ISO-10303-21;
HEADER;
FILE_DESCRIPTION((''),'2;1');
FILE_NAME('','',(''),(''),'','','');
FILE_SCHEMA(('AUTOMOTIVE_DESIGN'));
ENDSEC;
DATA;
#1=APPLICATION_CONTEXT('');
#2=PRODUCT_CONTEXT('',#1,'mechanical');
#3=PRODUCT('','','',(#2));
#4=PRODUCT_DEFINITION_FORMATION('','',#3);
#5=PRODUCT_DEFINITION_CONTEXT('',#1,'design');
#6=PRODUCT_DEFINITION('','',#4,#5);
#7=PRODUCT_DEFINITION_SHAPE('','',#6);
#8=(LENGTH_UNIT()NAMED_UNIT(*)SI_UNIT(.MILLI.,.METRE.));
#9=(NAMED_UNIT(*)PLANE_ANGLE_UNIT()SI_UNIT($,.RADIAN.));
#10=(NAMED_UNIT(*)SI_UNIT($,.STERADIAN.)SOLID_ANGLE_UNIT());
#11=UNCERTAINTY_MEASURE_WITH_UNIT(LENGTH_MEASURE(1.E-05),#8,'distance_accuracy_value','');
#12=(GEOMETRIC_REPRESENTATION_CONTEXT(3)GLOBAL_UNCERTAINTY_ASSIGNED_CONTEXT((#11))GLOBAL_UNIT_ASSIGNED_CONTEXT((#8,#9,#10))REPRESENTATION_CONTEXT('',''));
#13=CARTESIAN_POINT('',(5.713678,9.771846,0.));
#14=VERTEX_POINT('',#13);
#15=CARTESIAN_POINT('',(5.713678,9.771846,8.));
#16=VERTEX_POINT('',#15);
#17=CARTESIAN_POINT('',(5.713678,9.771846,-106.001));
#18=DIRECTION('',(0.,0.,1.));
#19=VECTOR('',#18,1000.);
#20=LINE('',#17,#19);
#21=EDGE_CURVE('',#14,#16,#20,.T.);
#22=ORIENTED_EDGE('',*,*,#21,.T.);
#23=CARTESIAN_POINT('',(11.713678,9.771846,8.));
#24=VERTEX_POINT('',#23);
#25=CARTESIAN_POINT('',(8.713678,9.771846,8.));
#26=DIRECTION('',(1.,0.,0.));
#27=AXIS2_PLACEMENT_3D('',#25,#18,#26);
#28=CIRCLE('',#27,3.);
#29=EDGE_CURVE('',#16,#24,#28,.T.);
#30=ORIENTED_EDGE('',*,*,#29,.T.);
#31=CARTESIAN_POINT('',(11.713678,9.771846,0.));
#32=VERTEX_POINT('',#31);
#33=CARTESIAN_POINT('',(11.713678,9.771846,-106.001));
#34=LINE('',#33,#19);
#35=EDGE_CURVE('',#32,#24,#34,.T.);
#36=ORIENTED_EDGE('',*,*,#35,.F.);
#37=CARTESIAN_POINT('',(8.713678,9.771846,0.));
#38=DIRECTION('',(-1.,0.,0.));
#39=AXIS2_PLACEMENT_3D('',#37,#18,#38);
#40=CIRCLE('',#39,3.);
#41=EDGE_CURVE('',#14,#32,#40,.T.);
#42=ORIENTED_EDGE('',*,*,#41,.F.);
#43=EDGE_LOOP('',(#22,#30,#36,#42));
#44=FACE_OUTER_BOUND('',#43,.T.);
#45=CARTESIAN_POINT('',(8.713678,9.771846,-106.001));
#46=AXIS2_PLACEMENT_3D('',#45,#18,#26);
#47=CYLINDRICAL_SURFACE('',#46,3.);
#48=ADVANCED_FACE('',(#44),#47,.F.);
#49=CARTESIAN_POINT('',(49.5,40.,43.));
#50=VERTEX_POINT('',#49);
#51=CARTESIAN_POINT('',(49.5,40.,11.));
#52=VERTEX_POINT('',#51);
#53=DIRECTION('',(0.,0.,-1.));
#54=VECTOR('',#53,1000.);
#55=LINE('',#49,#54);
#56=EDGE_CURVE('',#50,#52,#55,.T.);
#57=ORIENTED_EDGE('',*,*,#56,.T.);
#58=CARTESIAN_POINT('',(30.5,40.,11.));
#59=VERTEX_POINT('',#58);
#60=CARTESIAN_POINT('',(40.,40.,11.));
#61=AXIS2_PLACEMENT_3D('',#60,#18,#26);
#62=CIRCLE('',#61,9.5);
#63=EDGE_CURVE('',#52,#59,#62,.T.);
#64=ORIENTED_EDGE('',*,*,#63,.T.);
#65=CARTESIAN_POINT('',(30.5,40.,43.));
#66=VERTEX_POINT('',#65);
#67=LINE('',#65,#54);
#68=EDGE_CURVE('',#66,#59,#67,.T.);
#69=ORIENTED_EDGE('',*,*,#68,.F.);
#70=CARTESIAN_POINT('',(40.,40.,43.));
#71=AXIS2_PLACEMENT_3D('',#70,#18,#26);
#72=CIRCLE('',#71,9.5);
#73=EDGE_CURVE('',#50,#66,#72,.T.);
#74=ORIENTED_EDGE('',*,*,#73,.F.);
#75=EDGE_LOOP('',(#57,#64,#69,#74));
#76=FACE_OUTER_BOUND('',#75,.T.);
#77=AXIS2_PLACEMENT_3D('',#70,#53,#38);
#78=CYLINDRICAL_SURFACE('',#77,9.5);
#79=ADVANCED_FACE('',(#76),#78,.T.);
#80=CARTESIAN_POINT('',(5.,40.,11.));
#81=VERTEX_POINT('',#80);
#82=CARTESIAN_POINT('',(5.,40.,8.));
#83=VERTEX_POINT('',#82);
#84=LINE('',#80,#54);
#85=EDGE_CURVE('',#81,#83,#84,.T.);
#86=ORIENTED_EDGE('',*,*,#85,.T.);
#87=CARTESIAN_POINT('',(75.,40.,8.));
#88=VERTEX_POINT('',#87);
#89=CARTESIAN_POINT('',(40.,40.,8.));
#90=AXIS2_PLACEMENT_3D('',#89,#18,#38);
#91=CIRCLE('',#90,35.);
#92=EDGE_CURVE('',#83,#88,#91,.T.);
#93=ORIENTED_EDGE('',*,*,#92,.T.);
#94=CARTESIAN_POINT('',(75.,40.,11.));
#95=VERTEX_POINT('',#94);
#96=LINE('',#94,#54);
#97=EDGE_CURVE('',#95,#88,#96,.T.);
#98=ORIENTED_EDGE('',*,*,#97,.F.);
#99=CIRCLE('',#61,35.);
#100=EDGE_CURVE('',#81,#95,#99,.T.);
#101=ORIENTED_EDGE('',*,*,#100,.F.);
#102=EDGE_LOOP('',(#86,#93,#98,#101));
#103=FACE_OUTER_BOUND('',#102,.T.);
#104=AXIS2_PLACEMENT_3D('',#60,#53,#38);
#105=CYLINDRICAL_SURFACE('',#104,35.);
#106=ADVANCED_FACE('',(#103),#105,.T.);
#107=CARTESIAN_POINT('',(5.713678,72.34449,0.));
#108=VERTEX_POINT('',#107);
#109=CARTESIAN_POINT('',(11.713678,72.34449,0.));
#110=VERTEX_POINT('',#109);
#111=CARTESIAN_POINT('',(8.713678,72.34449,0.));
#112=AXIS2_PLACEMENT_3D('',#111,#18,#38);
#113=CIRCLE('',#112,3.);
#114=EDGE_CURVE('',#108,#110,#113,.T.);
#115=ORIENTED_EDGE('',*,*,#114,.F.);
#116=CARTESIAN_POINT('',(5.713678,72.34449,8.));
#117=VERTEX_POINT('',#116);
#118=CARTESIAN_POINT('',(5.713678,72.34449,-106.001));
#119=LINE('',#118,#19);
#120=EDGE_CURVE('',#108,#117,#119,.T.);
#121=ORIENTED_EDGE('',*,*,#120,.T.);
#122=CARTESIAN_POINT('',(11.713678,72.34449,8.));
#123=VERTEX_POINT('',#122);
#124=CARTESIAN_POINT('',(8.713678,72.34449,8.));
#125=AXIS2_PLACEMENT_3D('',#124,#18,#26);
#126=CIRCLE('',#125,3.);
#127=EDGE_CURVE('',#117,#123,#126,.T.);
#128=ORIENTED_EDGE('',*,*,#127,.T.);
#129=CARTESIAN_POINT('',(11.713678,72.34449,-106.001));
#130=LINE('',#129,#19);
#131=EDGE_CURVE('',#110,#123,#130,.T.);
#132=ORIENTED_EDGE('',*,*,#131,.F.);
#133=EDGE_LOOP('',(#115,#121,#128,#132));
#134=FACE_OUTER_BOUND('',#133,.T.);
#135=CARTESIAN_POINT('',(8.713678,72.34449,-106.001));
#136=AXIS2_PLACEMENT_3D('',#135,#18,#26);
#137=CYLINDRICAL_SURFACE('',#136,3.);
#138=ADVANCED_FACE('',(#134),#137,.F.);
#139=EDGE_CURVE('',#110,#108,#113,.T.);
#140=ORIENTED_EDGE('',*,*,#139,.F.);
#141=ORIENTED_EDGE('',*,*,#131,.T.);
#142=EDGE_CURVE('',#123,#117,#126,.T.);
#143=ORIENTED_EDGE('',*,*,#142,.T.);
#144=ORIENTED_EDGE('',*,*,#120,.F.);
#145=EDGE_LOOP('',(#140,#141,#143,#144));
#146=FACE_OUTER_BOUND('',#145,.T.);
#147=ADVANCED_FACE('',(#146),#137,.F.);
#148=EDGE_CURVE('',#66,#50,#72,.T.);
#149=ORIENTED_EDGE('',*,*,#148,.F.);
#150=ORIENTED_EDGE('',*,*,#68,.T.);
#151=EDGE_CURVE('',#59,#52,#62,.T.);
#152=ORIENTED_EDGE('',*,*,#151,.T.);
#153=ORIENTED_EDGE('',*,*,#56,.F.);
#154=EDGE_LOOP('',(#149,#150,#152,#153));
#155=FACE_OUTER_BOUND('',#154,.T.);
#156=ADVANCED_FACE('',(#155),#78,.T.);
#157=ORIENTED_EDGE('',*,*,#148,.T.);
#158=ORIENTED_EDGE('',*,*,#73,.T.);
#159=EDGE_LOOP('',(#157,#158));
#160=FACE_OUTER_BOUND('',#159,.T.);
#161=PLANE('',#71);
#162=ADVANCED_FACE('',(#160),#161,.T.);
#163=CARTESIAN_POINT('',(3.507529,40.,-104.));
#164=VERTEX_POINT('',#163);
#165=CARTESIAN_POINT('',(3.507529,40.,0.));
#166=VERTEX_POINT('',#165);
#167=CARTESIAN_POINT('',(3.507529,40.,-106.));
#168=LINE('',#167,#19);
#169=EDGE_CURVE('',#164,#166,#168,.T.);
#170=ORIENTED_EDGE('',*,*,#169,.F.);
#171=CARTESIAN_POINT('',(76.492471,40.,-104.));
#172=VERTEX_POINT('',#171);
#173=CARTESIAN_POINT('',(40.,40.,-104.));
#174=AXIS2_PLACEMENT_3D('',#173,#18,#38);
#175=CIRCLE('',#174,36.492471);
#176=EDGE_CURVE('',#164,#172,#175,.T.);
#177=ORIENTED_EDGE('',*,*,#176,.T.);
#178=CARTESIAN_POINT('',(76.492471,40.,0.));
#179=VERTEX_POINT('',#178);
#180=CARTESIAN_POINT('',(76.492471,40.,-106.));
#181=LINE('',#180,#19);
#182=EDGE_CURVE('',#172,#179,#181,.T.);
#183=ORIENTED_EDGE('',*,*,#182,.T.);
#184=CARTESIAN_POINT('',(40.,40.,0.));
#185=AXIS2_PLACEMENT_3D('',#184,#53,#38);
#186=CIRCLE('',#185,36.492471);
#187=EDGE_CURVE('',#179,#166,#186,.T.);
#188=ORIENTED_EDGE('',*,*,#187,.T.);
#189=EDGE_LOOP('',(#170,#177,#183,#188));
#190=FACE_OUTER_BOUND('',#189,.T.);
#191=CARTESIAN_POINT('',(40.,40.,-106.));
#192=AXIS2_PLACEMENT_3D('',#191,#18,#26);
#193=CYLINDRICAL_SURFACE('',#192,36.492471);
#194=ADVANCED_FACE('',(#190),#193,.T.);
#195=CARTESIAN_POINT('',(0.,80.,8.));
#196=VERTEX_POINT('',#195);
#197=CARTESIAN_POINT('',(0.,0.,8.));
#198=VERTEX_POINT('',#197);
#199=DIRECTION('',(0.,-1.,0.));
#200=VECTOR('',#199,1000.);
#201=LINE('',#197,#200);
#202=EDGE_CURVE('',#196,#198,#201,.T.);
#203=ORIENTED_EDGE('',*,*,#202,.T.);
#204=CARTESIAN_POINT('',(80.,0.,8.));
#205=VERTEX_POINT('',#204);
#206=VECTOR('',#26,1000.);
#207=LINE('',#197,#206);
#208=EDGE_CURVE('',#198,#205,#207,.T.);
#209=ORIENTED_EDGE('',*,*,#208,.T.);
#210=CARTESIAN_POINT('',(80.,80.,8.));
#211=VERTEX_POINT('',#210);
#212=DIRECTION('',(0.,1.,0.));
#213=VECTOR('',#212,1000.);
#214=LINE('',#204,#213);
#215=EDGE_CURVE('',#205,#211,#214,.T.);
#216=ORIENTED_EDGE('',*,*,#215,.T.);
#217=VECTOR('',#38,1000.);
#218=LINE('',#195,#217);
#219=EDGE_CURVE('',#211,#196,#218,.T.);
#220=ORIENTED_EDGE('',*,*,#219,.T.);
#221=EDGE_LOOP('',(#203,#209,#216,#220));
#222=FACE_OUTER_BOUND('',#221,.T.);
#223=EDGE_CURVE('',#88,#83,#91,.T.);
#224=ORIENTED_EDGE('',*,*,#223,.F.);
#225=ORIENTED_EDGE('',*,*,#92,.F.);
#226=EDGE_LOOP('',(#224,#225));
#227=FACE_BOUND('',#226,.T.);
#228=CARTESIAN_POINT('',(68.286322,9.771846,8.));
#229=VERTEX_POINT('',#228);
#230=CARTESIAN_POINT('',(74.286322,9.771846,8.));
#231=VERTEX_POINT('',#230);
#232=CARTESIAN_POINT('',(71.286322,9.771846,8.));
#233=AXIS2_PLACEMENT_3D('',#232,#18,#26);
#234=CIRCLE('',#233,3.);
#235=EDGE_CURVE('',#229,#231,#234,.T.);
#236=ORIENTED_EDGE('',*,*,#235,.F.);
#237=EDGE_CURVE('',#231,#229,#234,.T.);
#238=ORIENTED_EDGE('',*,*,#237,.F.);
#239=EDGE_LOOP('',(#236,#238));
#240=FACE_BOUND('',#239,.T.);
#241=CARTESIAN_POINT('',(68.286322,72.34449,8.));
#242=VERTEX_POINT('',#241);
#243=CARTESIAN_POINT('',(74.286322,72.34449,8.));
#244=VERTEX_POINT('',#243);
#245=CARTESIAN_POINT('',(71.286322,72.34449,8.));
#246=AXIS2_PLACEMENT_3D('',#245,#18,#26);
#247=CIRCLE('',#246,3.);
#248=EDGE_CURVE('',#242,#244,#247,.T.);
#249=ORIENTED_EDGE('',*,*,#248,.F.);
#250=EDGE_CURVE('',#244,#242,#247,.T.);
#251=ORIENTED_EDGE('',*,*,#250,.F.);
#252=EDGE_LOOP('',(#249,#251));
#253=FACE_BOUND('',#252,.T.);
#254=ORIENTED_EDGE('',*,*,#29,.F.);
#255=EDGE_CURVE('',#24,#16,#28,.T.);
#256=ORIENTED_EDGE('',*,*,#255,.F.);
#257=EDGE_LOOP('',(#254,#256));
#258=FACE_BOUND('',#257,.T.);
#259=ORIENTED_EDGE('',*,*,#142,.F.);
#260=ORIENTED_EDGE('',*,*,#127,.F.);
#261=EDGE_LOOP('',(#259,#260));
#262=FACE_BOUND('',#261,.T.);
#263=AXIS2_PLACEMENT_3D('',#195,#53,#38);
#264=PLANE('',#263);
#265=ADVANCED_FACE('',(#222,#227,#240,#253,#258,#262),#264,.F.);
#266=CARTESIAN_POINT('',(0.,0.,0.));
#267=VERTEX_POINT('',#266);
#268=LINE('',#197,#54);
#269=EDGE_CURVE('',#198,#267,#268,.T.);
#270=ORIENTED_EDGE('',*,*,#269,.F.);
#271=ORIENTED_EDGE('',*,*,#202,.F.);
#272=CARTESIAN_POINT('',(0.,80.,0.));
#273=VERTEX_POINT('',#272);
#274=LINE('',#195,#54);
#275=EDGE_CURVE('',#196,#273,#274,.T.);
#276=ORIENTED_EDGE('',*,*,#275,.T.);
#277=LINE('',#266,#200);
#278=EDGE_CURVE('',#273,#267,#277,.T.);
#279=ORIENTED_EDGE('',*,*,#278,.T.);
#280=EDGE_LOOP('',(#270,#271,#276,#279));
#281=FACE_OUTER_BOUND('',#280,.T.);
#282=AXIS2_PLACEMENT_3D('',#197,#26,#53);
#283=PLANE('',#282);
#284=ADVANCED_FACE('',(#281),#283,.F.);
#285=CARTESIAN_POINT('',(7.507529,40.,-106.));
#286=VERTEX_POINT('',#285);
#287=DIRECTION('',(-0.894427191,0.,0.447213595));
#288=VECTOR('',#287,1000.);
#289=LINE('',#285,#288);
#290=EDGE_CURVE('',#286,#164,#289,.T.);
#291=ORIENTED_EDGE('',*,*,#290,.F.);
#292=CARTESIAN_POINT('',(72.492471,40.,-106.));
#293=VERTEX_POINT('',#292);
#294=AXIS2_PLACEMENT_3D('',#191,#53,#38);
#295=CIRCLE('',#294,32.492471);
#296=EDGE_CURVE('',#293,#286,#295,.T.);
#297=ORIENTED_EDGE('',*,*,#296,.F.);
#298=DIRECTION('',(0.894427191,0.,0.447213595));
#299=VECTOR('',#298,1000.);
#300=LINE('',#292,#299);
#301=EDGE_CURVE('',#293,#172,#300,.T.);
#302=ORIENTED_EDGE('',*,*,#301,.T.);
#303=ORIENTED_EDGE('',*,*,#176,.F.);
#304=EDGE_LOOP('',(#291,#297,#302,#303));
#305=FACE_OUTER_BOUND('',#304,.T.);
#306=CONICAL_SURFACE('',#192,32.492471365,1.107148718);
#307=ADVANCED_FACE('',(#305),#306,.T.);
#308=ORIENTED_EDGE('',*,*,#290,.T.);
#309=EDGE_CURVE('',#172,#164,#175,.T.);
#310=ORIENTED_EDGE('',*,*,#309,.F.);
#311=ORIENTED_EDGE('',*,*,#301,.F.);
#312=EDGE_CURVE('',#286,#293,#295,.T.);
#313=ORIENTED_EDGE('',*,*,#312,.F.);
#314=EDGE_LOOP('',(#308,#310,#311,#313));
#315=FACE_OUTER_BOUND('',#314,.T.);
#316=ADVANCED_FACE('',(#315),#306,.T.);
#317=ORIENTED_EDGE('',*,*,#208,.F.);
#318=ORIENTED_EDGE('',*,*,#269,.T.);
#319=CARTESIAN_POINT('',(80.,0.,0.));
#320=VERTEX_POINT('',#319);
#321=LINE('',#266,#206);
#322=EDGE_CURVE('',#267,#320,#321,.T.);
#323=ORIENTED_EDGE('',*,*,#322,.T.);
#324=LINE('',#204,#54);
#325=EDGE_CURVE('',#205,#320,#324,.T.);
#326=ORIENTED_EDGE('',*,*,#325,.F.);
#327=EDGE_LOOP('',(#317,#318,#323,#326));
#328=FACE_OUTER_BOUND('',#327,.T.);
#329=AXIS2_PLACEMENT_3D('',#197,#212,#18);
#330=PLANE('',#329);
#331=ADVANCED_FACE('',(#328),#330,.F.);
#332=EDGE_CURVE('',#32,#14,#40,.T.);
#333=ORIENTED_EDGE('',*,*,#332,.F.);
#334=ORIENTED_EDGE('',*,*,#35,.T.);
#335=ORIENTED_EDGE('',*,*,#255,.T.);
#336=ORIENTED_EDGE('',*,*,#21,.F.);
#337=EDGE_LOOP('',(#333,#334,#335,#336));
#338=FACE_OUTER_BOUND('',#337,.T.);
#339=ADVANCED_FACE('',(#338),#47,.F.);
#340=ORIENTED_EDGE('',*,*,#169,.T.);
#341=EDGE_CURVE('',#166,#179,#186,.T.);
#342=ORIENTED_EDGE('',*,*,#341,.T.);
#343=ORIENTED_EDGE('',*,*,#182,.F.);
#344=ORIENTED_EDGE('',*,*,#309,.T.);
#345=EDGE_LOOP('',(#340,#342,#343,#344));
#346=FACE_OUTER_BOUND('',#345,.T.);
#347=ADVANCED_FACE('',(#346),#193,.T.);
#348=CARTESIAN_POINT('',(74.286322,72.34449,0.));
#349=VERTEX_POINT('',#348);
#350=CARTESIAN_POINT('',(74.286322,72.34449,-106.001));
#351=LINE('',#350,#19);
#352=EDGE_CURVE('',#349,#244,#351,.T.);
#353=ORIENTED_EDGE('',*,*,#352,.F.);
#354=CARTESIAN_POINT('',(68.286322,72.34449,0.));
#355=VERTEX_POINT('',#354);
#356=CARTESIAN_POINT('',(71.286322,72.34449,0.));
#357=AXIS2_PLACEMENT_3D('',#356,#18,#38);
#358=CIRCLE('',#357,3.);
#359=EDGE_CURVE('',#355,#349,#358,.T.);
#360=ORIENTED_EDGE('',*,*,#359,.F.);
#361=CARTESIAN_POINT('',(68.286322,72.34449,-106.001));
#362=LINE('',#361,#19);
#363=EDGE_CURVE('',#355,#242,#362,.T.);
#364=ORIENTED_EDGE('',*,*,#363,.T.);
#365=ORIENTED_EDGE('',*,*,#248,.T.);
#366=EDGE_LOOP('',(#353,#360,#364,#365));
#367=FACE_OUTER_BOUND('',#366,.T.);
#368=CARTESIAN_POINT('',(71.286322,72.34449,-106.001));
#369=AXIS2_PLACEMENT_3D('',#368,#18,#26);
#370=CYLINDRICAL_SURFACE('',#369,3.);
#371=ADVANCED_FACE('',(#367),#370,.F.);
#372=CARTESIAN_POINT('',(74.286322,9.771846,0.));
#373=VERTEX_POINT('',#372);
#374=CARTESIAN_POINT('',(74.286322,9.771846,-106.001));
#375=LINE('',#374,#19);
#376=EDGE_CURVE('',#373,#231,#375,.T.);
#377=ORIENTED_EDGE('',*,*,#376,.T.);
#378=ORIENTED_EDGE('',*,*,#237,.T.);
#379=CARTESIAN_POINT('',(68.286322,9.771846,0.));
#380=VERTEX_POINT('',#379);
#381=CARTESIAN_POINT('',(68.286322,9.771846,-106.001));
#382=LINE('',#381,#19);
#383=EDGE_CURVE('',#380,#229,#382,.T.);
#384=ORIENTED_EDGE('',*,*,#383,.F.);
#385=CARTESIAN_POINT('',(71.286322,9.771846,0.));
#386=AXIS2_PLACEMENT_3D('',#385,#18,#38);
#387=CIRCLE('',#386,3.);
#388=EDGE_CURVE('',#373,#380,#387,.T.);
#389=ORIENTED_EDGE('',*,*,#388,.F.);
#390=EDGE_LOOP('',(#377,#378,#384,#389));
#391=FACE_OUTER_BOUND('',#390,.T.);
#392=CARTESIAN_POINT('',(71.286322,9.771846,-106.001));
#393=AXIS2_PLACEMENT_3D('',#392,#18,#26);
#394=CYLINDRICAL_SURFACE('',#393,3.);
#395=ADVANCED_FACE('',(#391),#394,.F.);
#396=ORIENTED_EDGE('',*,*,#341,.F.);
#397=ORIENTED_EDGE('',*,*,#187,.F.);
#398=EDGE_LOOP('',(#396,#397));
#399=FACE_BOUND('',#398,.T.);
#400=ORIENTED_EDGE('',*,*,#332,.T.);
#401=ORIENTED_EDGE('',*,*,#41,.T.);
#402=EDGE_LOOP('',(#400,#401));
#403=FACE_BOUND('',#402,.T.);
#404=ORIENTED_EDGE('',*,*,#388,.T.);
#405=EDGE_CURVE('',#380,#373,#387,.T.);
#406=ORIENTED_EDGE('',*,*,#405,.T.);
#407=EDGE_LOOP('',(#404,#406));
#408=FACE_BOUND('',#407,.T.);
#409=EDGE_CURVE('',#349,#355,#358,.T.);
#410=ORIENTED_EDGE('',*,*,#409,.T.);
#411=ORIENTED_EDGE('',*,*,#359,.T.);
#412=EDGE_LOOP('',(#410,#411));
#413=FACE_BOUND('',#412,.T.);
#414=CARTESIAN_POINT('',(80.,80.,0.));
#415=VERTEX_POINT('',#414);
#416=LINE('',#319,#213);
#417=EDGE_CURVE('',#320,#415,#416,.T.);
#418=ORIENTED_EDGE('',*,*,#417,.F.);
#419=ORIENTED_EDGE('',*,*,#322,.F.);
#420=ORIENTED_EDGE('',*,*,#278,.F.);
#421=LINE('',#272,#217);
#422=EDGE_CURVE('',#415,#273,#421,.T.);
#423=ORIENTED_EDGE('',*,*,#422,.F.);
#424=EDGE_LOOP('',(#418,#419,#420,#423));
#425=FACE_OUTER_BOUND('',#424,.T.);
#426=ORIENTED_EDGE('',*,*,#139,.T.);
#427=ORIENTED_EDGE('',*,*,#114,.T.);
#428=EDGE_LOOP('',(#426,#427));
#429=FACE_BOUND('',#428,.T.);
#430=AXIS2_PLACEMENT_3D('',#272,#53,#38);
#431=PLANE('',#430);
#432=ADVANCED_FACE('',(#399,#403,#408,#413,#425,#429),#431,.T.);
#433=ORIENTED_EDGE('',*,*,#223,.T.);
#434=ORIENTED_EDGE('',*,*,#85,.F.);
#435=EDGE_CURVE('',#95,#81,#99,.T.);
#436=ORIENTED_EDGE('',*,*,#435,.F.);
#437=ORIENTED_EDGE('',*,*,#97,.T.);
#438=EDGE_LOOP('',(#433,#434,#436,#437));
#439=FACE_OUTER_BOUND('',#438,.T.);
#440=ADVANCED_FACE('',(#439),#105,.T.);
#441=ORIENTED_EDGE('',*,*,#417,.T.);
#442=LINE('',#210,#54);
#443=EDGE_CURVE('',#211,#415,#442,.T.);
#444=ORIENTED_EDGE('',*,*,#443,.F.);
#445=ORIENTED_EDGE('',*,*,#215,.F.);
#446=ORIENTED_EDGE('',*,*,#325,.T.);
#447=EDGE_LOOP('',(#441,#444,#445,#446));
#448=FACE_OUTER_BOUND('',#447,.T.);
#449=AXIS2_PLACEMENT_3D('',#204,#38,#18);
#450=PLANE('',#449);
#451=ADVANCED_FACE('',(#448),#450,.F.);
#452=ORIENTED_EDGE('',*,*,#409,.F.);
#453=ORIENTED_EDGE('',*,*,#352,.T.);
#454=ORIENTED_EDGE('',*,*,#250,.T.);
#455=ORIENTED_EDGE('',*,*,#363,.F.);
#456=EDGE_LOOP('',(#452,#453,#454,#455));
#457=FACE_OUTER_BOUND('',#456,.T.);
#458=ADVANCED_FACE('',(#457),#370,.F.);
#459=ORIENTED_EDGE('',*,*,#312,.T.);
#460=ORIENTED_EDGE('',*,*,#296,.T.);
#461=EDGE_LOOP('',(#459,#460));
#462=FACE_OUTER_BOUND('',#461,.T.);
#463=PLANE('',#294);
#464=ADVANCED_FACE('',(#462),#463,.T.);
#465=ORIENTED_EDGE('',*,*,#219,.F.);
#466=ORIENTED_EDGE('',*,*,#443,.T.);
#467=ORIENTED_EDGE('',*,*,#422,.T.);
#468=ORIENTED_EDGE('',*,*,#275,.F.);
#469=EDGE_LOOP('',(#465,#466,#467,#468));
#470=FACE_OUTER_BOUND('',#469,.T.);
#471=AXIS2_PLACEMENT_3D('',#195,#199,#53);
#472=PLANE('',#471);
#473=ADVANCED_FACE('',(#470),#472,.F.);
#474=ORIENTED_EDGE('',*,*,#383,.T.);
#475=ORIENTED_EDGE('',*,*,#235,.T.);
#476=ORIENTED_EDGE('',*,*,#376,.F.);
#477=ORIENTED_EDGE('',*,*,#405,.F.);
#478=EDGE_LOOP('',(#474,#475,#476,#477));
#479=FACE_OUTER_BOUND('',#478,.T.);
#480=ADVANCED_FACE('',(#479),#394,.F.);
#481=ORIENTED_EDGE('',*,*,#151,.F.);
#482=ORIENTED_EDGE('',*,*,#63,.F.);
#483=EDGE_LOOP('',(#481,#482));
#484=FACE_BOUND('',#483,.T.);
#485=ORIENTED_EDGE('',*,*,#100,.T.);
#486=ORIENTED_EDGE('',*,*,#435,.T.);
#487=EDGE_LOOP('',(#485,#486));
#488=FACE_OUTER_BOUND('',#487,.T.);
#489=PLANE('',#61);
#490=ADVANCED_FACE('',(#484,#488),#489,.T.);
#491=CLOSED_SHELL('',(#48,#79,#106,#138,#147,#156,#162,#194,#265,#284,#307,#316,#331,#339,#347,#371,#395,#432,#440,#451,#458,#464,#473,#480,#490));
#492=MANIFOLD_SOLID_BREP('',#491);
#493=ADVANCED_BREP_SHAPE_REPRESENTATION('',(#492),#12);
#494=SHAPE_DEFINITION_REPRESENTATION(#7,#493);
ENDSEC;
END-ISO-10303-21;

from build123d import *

# Parameters (mm, degrees)
SKETCH_1_W          = 80
SKETCH_1_H          = 80
EXTRUDE_1_DEPTH     = 8
SKETCH_2_R          = 35
EXTRUDE_2_DEPTH     = 3
SKETCH_3_R          = 9.5
EXTRUDE_3_DEPTH     = 32
SKETCH_4_R          = 36.492471365
EXTRUDE_4_DEPTH     = 106
CUT_EXTRUDE_1_REACH = 162.611
SKETCH_5_R          = 3
CHAMFER_1_SIZE      = 2
CHAMFER_1_SIZE2     = 4


with BuildPart() as part:
    # 草图1 → 拉伸1 (new body)
    with BuildSketch(Plane.XY):
        with Locations((40, 40)):
            Rectangle(SKETCH_1_W, SKETCH_1_H)
    extrude(amount=EXTRUDE_1_DEPTH)

    # 草图2 → 拉伸2 (add)
    with BuildSketch(Plane.XY.offset(8)):
        with Locations(Location((40, 40, 0), (0, 0, 180))):
            Circle(SKETCH_2_R)
    extrude(amount=EXTRUDE_2_DEPTH)

    # 草图3 → 拉伸3 (add)
    with BuildSketch(Plane.XY.offset(11)):
        with Locations((40, 40)):
            Circle(SKETCH_3_R)
    extrude(amount=EXTRUDE_3_DEPTH)

    # 草图4 → 拉伸4 (add)
    with BuildSketch(Plane(origin=(0, 0, 0), x_dir=(-1, 0, 0), z_dir=(0, 0, -1))):
        with Locations((-40, 40)):
            Circle(SKETCH_4_R)
    extrude(amount=EXTRUDE_4_DEPTH)

    # 草图5 → 切除-拉伸1 (cut, up to next)
    with BuildSketch(Plane.XY.offset(8), mode=Mode.PRIVATE) as cut_extrude_1_sk1:
        with Locations((8.713677805, 72.344490157)):
            Circle(SKETCH_5_R)
    cut_extrude_1_tool1 = extrude(cut_extrude_1_sk1.sketch, amount=-CUT_EXTRUDE_1_REACH, mode=Mode.PRIVATE) & part.part
    # 草图5 → 切除-拉伸1 (cut, up to next)
    with BuildSketch(Plane.XY.offset(8), mode=Mode.PRIVATE) as cut_extrude_1_sk2:
        with Locations((71.286322195, 72.344490157)):
            Circle(SKETCH_5_R)
    cut_extrude_1_tool2 = extrude(cut_extrude_1_sk2.sketch, amount=-CUT_EXTRUDE_1_REACH, mode=Mode.PRIVATE) & part.part
    # 草图5 → 切除-拉伸1 (cut, up to next)
    with BuildSketch(Plane.XY.offset(8), mode=Mode.PRIVATE) as cut_extrude_1_sk3:
        with Locations((71.286322195, 9.771845767)):
            Circle(SKETCH_5_R)
    cut_extrude_1_tool3 = extrude(cut_extrude_1_sk3.sketch, amount=-CUT_EXTRUDE_1_REACH, mode=Mode.PRIVATE) & part.part
    # 草图5 → 切除-拉伸1 (cut, up to next)
    with BuildSketch(Plane.XY.offset(8), mode=Mode.PRIVATE) as cut_extrude_1_sk4:
        with Locations((8.713677805, 9.771845767)):
            Circle(SKETCH_5_R)
    cut_extrude_1_tool4 = extrude(cut_extrude_1_sk4.sketch, amount=-CUT_EXTRUDE_1_REACH, mode=Mode.PRIVATE) & part.part
    add(cut_extrude_1_tool1.solids().sort_by_distance((8.713678, 72.34449, 8))[0], mode=Mode.SUBTRACT)
    add(cut_extrude_1_tool2.solids().sort_by_distance((71.286322, 72.34449, 8))[0], mode=Mode.SUBTRACT)
    add(cut_extrude_1_tool3.solids().sort_by_distance((71.286322, 9.771846, 8))[0], mode=Mode.SUBTRACT)
    add(cut_extrude_1_tool4.solids().sort_by_distance((8.713678, 9.771846, 8))[0], mode=Mode.SUBTRACT)

    # 倒角1
    chamfer_1_edges = [part.edges().sort_by_distance(p)[0] for p in [
        (76.492471365, 40, -106),
    ]]
    chamfer_1_side = [part.faces().sort_by_distance(p)[0] for p in [
        (76.492471365, 40, -53),
    ]]
    chamfer(chamfer_1_edges, length=CHAMFER_1_SIZE, length2=CHAMFER_1_SIZE2, reference=chamfer_1_side[0])


solid = part.part
